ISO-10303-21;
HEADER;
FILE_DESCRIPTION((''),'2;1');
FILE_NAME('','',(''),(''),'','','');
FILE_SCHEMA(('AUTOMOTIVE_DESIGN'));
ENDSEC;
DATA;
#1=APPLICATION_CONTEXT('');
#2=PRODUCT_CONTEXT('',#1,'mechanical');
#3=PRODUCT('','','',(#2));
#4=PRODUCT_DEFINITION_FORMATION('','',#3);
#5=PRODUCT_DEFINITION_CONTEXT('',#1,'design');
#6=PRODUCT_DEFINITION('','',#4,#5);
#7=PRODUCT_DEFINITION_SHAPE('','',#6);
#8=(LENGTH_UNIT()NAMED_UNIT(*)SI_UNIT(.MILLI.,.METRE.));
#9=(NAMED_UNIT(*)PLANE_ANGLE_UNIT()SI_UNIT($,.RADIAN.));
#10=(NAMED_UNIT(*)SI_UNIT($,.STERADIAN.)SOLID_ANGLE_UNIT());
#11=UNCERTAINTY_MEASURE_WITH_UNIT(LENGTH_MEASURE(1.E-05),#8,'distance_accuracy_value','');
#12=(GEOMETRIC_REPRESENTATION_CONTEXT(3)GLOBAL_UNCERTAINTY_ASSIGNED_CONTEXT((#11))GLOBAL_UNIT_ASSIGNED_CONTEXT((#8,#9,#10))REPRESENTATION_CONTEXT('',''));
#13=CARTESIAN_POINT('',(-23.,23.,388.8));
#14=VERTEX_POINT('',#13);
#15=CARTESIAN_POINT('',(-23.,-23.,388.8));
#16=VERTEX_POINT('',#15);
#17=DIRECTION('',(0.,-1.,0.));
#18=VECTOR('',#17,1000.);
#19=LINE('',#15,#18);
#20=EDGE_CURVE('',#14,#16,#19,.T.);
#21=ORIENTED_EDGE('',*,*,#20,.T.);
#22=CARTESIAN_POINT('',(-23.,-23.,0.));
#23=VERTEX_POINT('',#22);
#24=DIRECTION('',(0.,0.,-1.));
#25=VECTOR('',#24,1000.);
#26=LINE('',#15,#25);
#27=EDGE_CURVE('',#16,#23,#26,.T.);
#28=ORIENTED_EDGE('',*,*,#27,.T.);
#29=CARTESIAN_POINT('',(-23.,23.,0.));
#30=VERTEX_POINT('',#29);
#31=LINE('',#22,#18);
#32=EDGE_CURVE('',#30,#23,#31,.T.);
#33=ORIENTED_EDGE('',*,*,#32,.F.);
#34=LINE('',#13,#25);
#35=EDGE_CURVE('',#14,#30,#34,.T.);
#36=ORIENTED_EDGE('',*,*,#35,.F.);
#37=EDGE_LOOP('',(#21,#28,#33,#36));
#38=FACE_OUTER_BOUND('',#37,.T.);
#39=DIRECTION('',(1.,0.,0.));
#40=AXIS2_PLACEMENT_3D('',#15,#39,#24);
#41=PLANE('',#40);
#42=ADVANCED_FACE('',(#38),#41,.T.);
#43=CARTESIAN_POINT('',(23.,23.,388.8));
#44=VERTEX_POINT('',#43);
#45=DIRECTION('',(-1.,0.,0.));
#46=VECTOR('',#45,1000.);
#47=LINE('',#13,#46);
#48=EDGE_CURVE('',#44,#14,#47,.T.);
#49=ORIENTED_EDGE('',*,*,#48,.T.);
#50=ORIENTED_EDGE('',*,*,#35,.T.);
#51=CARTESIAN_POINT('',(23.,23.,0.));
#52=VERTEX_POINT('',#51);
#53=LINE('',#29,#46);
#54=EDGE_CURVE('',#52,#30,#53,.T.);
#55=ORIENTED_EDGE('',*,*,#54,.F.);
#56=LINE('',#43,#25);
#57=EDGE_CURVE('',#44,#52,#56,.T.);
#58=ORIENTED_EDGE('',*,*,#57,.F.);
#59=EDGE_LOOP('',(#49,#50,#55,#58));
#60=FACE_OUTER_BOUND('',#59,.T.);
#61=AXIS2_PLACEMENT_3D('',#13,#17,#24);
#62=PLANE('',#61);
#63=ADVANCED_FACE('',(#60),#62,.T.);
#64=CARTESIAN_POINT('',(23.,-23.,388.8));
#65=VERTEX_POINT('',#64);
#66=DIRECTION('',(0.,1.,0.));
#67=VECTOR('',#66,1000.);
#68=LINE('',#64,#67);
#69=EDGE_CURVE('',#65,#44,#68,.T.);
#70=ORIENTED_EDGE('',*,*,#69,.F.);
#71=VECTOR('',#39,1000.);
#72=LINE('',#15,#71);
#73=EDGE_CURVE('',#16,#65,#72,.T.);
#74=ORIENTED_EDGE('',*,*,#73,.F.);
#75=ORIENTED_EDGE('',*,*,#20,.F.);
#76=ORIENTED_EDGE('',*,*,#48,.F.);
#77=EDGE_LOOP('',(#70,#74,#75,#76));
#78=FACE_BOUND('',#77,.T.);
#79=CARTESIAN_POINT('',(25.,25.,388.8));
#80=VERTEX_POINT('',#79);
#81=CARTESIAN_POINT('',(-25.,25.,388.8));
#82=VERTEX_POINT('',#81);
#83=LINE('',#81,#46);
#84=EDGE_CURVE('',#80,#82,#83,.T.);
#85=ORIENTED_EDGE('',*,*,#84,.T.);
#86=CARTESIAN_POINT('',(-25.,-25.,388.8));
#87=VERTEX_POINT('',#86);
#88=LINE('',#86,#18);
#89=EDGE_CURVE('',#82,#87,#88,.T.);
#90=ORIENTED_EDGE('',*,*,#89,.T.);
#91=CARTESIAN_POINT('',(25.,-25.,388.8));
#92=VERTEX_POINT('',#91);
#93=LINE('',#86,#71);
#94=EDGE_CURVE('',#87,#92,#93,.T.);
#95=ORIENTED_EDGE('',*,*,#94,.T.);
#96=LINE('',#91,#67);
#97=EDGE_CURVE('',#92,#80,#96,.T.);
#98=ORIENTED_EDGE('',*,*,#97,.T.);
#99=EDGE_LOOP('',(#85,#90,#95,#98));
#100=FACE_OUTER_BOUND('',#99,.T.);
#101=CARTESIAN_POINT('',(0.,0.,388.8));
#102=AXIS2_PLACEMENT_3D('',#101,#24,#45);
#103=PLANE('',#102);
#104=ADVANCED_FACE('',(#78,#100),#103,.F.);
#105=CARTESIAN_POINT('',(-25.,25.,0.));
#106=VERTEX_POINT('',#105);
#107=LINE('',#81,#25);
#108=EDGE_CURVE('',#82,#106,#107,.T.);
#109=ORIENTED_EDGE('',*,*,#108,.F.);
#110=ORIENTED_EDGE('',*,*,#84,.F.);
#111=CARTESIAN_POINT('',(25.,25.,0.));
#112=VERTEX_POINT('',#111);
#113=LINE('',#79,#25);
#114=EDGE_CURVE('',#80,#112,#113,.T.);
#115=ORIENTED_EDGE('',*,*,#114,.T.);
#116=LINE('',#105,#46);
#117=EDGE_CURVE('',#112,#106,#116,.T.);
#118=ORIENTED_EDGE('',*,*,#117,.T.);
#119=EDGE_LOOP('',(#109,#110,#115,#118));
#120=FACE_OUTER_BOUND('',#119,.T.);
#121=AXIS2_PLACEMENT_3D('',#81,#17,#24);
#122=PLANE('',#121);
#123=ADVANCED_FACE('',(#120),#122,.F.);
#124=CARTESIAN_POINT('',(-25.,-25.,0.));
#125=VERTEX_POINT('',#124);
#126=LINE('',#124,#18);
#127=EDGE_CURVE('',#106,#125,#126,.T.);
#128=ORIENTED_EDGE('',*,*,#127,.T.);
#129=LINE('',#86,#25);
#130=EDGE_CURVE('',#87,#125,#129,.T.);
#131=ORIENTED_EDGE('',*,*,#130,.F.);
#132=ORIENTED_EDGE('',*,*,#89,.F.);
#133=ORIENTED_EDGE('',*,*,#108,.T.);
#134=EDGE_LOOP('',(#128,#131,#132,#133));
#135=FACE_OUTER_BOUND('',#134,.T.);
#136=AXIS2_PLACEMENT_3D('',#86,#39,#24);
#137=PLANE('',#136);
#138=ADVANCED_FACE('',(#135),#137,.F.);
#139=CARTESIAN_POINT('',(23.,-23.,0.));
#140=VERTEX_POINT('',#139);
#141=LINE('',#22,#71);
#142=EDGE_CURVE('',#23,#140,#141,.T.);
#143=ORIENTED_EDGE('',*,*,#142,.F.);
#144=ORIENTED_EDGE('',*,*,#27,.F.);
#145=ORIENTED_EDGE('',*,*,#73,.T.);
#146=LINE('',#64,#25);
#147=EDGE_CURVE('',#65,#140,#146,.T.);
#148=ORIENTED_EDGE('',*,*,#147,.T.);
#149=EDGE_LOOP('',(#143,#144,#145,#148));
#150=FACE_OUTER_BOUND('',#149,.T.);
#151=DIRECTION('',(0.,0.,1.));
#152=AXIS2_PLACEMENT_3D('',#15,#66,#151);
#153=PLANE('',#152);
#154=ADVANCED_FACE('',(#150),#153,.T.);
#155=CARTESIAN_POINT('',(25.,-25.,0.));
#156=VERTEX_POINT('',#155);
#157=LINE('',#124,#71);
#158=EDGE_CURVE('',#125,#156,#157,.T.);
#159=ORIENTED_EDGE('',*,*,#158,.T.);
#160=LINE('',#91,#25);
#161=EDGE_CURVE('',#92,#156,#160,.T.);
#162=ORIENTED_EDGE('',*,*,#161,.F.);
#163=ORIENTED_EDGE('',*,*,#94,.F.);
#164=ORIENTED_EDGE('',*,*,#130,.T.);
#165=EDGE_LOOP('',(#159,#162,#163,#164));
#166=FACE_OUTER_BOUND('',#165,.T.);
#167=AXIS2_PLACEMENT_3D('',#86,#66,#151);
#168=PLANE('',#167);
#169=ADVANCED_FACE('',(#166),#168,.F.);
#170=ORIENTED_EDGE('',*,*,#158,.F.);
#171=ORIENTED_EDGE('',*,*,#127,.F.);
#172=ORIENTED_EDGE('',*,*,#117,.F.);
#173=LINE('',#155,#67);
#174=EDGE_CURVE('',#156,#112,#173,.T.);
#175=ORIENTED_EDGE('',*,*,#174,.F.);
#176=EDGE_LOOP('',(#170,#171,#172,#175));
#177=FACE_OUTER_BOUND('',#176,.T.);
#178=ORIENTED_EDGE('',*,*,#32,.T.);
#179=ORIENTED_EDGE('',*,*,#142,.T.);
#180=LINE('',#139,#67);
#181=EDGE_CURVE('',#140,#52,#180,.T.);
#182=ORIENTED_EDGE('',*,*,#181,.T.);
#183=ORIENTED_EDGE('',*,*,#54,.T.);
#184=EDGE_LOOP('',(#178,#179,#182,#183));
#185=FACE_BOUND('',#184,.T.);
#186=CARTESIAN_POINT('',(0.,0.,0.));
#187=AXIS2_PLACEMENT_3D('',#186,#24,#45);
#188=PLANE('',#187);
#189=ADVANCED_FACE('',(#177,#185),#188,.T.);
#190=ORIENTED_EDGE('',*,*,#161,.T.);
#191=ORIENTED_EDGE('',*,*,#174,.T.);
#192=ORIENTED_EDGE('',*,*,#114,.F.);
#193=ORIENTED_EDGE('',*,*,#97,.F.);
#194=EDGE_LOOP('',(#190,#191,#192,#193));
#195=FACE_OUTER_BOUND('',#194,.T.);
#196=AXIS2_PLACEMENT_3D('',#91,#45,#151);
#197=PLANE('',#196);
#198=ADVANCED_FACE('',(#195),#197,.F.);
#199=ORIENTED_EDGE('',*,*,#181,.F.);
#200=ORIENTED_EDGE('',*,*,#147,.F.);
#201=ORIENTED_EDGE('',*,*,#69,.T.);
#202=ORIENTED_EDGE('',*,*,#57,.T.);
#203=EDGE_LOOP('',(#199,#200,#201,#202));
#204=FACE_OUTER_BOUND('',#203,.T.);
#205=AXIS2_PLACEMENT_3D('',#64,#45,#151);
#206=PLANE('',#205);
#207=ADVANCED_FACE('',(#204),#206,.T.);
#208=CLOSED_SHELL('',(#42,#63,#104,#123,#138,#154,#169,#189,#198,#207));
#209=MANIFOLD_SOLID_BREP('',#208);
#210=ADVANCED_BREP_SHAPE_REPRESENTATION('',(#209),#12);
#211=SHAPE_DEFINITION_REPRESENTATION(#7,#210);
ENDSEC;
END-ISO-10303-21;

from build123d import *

# Parameters (mm, degrees)
SKETCH1_W           = 50
SKETCH1_H           = 50
SKETCH1_W_2         = 46
SKETCH1_H_2         = 46
BOSS_EXTRUDE1_DEPTH = 388.8


with BuildPart() as part:
    # Sketch1 → Boss-Extrude1 (new body)
    with BuildSketch(Plane.XY):
        Rectangle(SKETCH1_W, SKETCH1_H)
        Rectangle(SKETCH1_W_2, SKETCH1_H_2, mode=Mode.SUBTRACT)
    extrude(amount=BOSS_EXTRUDE1_DEPTH)


solid = part.part
